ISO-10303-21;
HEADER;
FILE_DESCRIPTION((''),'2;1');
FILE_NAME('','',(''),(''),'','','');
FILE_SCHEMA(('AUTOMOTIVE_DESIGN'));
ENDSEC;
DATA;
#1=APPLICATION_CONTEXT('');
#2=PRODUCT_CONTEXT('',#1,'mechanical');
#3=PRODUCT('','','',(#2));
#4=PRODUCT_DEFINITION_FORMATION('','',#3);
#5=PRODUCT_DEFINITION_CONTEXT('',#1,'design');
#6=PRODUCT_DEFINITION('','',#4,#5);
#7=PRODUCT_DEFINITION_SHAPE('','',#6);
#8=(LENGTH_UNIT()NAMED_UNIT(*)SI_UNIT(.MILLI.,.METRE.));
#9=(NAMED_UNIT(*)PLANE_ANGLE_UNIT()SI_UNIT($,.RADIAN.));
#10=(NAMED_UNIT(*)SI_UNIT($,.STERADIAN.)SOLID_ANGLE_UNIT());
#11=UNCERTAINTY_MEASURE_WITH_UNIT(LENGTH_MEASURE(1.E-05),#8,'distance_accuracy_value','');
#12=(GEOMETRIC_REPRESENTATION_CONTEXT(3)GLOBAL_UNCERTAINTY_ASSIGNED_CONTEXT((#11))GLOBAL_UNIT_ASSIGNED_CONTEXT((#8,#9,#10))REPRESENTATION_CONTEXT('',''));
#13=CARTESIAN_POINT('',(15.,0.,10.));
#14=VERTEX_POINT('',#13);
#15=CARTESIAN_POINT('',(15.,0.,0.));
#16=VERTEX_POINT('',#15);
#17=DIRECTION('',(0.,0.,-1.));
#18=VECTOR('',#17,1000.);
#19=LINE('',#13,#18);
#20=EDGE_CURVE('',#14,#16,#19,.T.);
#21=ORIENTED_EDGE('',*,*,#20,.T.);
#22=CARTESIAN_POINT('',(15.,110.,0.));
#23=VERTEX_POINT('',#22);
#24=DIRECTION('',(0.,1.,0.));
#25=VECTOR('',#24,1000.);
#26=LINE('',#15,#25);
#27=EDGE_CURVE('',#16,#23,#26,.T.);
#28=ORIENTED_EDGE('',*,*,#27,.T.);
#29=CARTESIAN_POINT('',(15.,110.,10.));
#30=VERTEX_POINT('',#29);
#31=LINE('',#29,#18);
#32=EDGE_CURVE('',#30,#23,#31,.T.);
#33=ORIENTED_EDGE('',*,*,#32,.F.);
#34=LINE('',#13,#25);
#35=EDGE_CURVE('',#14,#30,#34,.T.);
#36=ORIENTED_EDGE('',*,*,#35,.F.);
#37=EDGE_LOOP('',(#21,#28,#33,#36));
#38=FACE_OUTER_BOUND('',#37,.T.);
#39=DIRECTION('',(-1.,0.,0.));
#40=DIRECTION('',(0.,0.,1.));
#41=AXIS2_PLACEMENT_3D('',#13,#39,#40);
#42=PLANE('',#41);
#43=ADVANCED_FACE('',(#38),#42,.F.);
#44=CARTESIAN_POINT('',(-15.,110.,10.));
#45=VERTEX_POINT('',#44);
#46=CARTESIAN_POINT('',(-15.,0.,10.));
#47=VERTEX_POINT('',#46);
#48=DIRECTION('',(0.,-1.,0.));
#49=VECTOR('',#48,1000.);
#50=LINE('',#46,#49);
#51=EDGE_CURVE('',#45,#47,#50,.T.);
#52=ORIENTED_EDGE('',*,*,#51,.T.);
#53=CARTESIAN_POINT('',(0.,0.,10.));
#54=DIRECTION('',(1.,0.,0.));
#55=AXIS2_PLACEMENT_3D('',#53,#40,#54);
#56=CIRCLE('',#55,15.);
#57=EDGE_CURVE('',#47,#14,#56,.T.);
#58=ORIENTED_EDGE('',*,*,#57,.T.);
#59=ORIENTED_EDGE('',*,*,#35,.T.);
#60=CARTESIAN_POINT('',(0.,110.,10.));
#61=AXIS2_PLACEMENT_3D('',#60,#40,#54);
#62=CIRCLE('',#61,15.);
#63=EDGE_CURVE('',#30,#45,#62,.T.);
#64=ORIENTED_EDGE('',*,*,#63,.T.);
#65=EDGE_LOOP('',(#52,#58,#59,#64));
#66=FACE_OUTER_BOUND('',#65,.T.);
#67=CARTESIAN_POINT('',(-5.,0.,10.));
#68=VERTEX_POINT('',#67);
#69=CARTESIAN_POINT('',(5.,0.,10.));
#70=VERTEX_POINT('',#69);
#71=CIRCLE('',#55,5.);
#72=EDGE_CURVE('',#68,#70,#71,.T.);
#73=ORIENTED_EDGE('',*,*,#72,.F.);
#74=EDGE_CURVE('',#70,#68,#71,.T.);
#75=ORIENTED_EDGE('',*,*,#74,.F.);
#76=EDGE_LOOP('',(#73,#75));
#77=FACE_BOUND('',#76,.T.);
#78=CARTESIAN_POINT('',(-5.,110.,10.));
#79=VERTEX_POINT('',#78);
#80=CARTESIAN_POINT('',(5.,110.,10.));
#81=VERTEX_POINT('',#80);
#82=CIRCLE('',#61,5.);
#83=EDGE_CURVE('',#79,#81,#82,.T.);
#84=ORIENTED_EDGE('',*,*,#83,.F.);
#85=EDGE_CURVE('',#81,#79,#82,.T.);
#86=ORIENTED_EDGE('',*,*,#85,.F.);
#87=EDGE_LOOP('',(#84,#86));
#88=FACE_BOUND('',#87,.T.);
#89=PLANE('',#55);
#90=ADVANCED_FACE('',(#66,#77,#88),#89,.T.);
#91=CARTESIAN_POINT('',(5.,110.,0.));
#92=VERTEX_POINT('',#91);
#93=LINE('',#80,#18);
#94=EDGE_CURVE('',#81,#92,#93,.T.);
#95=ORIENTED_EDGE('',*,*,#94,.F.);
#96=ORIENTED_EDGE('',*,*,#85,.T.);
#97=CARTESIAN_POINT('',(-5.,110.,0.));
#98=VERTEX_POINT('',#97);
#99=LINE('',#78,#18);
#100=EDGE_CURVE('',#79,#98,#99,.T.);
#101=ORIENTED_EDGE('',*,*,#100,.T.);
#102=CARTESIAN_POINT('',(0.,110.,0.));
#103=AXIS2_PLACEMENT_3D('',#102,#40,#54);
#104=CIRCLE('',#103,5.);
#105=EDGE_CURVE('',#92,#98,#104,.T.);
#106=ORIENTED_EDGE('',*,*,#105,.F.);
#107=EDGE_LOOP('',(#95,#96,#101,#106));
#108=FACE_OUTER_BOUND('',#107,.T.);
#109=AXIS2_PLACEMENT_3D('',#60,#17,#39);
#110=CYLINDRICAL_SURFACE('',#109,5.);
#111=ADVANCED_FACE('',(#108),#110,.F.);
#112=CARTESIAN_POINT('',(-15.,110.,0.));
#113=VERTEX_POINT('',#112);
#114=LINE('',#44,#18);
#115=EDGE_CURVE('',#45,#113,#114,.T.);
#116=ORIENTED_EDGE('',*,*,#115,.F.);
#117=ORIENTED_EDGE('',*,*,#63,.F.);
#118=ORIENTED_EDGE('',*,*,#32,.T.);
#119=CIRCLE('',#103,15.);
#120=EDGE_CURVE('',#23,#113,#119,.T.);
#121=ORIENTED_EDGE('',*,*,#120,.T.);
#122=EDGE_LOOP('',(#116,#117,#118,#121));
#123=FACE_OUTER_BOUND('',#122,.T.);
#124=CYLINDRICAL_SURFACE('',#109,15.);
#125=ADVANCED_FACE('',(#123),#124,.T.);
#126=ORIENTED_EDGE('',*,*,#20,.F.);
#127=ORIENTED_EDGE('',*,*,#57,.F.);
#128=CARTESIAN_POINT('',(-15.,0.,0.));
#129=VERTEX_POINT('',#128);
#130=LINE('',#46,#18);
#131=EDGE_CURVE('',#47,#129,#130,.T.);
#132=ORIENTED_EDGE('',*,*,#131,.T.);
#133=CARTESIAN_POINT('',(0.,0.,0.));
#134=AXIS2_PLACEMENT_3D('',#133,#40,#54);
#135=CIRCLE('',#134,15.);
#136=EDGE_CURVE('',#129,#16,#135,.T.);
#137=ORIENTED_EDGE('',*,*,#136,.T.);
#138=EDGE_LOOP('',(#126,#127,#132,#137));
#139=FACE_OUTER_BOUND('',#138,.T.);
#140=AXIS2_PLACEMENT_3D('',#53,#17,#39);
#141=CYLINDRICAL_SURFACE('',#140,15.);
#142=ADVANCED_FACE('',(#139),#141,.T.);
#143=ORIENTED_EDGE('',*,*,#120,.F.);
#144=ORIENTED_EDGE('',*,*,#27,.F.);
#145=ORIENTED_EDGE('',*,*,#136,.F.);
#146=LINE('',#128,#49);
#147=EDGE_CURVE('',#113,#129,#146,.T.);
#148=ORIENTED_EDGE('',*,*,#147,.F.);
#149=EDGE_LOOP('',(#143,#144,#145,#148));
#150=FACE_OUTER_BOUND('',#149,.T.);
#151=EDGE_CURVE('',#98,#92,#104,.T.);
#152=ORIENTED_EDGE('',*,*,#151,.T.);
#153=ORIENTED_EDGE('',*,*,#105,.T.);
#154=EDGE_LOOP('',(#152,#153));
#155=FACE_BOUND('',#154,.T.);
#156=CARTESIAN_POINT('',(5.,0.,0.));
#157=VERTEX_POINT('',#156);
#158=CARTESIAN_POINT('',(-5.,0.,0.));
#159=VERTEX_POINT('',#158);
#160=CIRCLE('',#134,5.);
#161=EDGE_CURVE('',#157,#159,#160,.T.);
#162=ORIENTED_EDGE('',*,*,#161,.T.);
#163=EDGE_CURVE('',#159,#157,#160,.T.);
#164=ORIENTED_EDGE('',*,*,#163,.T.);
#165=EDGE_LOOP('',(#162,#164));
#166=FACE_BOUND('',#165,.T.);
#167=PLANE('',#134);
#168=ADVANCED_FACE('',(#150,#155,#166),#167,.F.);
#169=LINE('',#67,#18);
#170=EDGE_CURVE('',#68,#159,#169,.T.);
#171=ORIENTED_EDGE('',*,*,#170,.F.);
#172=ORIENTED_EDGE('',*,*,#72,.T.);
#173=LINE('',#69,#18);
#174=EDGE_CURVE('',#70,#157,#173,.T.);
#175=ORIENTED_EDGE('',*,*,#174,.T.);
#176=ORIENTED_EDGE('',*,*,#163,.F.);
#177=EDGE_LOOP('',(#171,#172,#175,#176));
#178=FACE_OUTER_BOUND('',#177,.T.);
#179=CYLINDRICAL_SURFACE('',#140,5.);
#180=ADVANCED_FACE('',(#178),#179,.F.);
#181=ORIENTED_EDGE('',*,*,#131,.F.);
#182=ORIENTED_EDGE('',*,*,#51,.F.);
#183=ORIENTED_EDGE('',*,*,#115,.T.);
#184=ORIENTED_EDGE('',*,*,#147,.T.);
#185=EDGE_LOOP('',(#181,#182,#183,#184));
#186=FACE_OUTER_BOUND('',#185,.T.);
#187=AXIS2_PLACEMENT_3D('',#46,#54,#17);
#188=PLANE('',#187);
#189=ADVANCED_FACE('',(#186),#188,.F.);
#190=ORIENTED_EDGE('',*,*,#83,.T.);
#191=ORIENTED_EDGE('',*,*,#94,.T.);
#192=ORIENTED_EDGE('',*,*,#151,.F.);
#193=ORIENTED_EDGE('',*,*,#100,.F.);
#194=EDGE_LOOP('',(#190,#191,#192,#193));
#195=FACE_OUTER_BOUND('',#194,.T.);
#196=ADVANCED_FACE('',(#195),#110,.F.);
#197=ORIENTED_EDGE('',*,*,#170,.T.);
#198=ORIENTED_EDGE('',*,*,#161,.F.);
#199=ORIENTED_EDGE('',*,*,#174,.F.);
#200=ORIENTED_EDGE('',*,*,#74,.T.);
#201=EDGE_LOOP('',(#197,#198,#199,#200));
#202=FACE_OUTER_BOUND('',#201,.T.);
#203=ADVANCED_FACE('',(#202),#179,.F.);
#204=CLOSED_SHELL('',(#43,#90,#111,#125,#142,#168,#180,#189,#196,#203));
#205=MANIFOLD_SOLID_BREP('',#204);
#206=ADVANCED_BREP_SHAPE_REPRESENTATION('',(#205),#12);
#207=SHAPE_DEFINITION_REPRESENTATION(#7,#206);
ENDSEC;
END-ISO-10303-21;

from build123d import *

# Parameters (mm, degrees)
SKETCH_1_R      = 5
EXTRUDE_1_DEPTH = 10


with BuildPart() as part:
    # 草图1 → 凸台-拉伸1 (new body)
    with BuildSketch(Plane.XY):
        with BuildLine():
            Line((-15, 0), (-15, 110))
            ThreePointArc((-15, 110), (0, 125), (15, 110))
            Line((15, 110), (15, 0))
            ThreePointArc((15, 0), (0, -15), (-15, 0))
        make_face()
        Circle(SKETCH_1_R, mode=Mode.SUBTRACT)
        with Locations((0, 110)):
            Circle(SKETCH_1_R, mode=Mode.SUBTRACT)
    extrude(amount=EXTRUDE_1_DEPTH)


solid = part.part
